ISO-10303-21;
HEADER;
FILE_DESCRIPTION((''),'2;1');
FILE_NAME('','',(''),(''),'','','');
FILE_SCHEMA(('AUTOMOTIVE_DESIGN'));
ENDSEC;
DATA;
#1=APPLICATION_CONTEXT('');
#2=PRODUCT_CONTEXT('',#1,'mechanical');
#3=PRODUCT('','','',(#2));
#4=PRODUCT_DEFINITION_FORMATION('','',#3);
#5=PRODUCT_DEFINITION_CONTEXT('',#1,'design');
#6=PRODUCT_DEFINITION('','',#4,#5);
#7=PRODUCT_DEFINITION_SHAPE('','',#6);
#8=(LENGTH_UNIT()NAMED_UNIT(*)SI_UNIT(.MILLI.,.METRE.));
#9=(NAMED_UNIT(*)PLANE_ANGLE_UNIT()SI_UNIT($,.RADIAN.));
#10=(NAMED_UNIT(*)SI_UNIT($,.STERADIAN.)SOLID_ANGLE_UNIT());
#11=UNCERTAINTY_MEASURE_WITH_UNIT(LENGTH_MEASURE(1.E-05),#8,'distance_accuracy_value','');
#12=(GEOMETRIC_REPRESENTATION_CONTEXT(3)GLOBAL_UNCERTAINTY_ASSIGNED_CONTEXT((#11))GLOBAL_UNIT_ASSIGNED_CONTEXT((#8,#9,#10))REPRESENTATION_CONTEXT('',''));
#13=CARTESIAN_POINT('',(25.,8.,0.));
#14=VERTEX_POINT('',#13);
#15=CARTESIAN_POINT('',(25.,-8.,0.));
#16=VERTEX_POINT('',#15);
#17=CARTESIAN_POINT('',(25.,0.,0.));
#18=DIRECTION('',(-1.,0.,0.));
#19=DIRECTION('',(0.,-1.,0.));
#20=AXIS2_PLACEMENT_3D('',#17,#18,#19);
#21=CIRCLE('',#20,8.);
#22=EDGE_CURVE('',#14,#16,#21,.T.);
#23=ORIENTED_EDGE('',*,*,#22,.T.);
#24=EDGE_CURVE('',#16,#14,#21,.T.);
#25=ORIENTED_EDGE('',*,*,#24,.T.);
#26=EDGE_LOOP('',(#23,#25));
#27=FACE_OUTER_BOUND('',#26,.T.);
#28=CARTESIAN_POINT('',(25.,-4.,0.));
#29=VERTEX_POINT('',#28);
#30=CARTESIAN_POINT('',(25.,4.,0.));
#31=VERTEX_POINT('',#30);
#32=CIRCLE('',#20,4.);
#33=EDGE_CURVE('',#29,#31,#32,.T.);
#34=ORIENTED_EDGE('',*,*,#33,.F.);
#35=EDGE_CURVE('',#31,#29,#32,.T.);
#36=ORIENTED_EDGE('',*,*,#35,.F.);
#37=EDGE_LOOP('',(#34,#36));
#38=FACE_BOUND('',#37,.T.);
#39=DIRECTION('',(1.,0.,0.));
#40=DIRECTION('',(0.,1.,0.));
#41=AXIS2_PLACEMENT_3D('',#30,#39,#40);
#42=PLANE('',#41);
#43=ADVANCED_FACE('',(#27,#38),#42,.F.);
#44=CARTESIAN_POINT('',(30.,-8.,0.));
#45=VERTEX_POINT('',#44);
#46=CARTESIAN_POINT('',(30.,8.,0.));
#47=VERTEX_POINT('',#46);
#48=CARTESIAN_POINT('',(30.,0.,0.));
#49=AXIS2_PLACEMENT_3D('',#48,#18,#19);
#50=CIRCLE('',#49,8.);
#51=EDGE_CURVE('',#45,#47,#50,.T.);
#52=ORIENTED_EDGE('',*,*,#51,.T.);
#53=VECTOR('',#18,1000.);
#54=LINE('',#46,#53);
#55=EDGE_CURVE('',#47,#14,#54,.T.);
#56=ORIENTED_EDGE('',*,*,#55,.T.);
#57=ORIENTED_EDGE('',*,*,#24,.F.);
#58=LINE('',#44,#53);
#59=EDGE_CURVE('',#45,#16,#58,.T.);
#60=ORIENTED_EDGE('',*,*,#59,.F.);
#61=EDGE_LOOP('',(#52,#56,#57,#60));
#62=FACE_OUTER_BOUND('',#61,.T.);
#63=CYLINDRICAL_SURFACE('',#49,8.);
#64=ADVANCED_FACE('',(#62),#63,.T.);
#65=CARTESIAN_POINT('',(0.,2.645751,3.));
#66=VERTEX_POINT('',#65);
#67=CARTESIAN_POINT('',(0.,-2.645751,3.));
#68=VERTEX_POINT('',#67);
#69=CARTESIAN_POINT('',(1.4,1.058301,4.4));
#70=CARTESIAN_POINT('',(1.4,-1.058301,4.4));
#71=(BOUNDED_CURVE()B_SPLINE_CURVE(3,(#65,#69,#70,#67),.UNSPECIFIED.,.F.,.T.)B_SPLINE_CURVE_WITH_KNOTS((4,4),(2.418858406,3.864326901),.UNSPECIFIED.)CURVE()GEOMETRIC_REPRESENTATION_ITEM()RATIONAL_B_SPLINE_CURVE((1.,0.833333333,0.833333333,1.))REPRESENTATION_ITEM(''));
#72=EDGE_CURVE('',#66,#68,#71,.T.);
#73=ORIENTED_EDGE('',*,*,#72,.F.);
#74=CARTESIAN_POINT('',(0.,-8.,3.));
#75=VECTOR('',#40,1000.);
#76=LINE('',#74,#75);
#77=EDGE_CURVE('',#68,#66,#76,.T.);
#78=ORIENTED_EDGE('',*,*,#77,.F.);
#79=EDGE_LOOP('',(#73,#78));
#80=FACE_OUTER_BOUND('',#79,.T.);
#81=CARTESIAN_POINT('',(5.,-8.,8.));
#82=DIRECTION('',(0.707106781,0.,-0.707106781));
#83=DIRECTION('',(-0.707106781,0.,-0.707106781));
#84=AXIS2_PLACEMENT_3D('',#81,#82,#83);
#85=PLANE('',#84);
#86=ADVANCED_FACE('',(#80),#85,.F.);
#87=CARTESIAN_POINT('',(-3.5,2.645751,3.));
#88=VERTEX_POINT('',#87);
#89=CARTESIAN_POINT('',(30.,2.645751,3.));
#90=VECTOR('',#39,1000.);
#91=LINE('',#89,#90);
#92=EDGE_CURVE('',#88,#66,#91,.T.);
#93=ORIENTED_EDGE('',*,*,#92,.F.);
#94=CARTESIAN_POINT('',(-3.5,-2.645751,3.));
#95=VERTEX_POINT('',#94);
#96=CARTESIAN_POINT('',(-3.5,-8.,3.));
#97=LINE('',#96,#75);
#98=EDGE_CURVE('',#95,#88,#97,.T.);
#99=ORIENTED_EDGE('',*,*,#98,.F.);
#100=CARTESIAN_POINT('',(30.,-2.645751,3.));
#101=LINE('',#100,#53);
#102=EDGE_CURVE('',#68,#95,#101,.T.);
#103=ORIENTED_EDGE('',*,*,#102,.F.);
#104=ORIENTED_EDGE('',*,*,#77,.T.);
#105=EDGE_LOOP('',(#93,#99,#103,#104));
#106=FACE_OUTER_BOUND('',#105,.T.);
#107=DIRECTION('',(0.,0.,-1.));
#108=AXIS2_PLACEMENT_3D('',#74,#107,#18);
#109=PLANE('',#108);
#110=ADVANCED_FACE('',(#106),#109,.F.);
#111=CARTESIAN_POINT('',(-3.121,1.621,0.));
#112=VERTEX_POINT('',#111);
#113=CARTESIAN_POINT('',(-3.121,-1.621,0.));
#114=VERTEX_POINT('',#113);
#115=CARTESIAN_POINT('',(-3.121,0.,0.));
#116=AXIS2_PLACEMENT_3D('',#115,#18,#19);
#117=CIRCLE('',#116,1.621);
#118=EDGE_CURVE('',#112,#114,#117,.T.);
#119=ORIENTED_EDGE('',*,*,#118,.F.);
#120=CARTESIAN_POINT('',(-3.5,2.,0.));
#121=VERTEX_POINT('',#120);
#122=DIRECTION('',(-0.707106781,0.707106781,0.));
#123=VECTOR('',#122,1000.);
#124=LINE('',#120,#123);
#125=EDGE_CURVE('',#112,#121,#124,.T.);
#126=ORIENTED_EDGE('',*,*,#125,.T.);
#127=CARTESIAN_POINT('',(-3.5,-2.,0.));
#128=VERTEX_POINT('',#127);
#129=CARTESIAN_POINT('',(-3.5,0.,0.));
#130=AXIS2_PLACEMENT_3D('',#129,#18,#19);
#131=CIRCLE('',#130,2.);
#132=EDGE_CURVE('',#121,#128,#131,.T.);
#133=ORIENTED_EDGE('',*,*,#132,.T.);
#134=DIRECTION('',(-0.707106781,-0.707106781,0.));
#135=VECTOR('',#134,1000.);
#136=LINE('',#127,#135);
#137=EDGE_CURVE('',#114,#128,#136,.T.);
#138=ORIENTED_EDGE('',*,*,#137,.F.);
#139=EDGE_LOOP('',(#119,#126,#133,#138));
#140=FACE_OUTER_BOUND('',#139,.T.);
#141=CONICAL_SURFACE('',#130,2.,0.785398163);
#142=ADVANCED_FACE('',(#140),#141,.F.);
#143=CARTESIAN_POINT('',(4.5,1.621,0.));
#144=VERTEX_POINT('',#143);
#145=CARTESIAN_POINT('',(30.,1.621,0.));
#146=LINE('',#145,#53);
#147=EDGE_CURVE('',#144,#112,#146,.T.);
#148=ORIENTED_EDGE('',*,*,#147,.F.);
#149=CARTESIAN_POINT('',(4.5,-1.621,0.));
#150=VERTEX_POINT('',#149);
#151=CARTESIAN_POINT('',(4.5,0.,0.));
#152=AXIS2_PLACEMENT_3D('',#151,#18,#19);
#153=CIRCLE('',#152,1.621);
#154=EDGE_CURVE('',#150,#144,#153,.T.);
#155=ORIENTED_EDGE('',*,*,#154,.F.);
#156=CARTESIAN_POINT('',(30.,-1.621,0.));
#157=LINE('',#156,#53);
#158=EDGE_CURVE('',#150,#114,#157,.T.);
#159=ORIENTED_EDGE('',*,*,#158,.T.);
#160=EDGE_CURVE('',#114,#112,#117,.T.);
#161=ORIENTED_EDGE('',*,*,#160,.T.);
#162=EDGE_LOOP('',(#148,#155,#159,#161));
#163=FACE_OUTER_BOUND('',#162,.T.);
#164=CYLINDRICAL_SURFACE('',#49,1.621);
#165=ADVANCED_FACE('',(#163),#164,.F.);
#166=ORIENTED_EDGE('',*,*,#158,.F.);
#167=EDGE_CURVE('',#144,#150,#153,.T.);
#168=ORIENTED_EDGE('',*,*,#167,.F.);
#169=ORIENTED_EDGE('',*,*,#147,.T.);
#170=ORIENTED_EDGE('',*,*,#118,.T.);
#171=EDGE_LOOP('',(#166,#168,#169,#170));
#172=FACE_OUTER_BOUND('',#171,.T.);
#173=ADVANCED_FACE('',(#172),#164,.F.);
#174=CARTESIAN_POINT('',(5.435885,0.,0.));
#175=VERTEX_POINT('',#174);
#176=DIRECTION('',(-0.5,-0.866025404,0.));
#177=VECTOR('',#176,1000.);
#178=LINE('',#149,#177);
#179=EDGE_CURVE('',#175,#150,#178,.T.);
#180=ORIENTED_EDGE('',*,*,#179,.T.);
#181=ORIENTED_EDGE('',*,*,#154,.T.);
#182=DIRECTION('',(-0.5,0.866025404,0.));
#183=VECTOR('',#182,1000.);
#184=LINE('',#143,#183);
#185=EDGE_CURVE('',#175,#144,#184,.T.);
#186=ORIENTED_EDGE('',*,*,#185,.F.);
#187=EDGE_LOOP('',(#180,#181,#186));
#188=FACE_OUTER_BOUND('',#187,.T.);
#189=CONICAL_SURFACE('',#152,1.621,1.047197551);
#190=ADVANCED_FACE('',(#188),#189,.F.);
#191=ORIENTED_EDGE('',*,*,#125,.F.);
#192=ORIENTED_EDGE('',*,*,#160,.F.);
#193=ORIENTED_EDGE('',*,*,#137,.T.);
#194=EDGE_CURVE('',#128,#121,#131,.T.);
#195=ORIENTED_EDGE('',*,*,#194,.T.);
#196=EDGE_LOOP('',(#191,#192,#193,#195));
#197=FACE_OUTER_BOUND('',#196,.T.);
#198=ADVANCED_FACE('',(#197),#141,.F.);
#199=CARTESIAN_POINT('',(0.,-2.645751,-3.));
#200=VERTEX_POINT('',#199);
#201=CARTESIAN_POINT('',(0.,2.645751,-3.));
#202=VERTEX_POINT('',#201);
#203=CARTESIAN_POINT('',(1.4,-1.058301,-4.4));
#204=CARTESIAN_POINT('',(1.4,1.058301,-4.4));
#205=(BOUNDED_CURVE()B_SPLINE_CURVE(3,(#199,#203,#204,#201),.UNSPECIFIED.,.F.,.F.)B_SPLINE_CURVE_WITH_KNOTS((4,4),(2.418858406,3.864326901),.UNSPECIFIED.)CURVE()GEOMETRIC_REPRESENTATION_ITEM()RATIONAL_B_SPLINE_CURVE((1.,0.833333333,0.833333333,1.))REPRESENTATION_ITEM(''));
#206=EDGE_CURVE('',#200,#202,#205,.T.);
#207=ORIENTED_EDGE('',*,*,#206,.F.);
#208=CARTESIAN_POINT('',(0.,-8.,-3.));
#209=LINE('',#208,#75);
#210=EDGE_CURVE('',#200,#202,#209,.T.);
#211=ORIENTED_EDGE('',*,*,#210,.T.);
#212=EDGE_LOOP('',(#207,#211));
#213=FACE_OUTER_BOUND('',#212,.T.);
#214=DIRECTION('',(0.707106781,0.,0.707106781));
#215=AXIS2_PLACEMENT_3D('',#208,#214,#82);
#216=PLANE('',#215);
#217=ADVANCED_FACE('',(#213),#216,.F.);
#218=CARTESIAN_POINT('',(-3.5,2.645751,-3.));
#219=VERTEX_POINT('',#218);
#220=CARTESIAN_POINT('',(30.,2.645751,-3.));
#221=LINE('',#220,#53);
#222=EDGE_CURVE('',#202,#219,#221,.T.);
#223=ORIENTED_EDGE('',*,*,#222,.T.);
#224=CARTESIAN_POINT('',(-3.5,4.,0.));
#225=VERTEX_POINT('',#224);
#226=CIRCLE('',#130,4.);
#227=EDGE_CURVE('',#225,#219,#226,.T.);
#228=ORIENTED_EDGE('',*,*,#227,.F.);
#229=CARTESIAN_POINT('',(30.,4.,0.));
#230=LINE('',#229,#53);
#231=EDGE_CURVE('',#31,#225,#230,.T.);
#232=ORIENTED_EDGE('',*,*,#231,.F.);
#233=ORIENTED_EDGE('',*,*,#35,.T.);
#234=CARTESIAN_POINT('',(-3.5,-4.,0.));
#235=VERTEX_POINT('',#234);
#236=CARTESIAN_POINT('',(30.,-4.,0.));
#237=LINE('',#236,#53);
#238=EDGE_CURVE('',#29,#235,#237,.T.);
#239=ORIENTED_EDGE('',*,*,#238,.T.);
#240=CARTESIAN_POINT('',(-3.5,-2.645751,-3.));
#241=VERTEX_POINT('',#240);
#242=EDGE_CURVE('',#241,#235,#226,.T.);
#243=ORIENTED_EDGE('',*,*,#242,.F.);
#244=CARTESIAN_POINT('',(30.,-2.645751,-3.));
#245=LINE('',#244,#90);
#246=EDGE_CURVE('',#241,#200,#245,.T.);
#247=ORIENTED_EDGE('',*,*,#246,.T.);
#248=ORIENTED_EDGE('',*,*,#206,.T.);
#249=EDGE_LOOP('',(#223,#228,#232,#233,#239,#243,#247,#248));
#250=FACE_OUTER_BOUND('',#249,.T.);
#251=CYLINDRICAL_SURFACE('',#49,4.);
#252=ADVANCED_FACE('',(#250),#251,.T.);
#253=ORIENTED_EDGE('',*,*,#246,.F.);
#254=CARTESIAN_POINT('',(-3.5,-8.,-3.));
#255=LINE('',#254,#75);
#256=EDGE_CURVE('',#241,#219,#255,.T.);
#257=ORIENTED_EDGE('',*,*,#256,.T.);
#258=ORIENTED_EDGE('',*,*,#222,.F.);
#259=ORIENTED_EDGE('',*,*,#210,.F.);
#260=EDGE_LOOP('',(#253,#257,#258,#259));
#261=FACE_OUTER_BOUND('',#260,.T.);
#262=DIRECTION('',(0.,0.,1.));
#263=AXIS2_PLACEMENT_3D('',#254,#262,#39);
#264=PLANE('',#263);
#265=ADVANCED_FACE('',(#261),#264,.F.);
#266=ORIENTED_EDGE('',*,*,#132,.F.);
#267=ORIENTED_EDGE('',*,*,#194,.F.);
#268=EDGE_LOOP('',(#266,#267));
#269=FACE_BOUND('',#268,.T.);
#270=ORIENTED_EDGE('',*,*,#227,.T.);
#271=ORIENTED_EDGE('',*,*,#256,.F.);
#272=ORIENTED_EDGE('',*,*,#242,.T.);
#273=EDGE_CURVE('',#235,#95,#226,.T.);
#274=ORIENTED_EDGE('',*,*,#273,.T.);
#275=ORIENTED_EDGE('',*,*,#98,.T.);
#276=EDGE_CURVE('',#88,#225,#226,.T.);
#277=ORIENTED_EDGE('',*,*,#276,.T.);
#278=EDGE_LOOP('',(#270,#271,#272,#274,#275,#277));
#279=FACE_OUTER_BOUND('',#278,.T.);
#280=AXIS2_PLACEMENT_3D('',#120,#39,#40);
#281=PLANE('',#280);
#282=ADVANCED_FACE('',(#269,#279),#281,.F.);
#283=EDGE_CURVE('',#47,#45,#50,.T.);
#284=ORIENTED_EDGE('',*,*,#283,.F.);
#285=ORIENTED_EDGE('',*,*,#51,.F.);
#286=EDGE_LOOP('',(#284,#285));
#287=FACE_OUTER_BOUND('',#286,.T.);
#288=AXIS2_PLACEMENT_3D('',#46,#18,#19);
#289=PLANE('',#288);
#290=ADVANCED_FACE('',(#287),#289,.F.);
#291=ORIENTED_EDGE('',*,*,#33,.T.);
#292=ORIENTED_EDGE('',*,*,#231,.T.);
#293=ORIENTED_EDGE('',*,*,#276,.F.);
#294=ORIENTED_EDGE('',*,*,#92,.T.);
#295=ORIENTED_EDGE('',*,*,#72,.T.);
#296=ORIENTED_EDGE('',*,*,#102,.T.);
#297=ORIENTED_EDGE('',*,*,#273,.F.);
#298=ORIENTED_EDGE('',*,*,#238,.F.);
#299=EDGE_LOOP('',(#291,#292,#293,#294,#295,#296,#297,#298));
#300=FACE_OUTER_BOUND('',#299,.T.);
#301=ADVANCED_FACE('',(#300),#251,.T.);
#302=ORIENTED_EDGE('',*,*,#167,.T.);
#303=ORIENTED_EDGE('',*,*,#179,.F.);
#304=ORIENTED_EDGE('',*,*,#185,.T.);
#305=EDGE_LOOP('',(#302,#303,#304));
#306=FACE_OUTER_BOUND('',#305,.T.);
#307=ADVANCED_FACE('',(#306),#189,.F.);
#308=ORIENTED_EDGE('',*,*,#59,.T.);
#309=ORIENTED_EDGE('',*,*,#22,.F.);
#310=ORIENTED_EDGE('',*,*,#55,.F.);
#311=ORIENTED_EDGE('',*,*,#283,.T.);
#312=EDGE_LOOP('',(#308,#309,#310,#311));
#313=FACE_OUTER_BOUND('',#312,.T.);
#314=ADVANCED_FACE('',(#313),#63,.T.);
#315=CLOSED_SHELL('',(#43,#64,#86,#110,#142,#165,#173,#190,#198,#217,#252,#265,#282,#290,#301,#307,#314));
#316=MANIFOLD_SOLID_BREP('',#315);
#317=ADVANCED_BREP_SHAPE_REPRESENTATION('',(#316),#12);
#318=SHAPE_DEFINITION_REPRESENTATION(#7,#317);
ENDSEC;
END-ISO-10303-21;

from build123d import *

# Parameters (mm, degrees)
CUT_EXTRUDE1_DEPTH      = 8
CUT_EXTRUDE1_DEPTH_BACK = 8


with BuildPart() as part:
    # Sketch1 → Revolve1 (revolve)
    with BuildSketch(Plane.XY, mode=Mode.PRIVATE) as revolve1_sk:
        Polygon((5.435884786, 0), (4.5, 1.621), (-3.121, 1.621), (-3.5, 2), (-3.5, 4), (25, 4), (25, 8), (30, 8), (30, 0), align=None)
    revolve(revolve1_sk.sketch.rotate(Axis((30, 0, 0), (-1, 0, 0)), 180), axis=Axis((30, 0, 0), (-1, 0, 0)))

    # Sketch2 → Cut-Extrude1 (cut, two sides: drawn at the far end of the back side and taken through both)
    with BuildSketch(Plane(origin=(0, 0, 0), x_dir=(1, 0, 0), z_dir=(0, 1, 0)).offset(-CUT_EXTRUDE1_DEPTH_BACK)):
        Polygon((-8.5, 8), (-8.5, -8), (5, -8), (0, -3), (-3.5, -3), (-3.5, 3), (0, 3), (5, 8), align=None)
    extrude(amount=CUT_EXTRUDE1_DEPTH + CUT_EXTRUDE1_DEPTH_BACK, mode=Mode.SUBTRACT)


solid = part.part
